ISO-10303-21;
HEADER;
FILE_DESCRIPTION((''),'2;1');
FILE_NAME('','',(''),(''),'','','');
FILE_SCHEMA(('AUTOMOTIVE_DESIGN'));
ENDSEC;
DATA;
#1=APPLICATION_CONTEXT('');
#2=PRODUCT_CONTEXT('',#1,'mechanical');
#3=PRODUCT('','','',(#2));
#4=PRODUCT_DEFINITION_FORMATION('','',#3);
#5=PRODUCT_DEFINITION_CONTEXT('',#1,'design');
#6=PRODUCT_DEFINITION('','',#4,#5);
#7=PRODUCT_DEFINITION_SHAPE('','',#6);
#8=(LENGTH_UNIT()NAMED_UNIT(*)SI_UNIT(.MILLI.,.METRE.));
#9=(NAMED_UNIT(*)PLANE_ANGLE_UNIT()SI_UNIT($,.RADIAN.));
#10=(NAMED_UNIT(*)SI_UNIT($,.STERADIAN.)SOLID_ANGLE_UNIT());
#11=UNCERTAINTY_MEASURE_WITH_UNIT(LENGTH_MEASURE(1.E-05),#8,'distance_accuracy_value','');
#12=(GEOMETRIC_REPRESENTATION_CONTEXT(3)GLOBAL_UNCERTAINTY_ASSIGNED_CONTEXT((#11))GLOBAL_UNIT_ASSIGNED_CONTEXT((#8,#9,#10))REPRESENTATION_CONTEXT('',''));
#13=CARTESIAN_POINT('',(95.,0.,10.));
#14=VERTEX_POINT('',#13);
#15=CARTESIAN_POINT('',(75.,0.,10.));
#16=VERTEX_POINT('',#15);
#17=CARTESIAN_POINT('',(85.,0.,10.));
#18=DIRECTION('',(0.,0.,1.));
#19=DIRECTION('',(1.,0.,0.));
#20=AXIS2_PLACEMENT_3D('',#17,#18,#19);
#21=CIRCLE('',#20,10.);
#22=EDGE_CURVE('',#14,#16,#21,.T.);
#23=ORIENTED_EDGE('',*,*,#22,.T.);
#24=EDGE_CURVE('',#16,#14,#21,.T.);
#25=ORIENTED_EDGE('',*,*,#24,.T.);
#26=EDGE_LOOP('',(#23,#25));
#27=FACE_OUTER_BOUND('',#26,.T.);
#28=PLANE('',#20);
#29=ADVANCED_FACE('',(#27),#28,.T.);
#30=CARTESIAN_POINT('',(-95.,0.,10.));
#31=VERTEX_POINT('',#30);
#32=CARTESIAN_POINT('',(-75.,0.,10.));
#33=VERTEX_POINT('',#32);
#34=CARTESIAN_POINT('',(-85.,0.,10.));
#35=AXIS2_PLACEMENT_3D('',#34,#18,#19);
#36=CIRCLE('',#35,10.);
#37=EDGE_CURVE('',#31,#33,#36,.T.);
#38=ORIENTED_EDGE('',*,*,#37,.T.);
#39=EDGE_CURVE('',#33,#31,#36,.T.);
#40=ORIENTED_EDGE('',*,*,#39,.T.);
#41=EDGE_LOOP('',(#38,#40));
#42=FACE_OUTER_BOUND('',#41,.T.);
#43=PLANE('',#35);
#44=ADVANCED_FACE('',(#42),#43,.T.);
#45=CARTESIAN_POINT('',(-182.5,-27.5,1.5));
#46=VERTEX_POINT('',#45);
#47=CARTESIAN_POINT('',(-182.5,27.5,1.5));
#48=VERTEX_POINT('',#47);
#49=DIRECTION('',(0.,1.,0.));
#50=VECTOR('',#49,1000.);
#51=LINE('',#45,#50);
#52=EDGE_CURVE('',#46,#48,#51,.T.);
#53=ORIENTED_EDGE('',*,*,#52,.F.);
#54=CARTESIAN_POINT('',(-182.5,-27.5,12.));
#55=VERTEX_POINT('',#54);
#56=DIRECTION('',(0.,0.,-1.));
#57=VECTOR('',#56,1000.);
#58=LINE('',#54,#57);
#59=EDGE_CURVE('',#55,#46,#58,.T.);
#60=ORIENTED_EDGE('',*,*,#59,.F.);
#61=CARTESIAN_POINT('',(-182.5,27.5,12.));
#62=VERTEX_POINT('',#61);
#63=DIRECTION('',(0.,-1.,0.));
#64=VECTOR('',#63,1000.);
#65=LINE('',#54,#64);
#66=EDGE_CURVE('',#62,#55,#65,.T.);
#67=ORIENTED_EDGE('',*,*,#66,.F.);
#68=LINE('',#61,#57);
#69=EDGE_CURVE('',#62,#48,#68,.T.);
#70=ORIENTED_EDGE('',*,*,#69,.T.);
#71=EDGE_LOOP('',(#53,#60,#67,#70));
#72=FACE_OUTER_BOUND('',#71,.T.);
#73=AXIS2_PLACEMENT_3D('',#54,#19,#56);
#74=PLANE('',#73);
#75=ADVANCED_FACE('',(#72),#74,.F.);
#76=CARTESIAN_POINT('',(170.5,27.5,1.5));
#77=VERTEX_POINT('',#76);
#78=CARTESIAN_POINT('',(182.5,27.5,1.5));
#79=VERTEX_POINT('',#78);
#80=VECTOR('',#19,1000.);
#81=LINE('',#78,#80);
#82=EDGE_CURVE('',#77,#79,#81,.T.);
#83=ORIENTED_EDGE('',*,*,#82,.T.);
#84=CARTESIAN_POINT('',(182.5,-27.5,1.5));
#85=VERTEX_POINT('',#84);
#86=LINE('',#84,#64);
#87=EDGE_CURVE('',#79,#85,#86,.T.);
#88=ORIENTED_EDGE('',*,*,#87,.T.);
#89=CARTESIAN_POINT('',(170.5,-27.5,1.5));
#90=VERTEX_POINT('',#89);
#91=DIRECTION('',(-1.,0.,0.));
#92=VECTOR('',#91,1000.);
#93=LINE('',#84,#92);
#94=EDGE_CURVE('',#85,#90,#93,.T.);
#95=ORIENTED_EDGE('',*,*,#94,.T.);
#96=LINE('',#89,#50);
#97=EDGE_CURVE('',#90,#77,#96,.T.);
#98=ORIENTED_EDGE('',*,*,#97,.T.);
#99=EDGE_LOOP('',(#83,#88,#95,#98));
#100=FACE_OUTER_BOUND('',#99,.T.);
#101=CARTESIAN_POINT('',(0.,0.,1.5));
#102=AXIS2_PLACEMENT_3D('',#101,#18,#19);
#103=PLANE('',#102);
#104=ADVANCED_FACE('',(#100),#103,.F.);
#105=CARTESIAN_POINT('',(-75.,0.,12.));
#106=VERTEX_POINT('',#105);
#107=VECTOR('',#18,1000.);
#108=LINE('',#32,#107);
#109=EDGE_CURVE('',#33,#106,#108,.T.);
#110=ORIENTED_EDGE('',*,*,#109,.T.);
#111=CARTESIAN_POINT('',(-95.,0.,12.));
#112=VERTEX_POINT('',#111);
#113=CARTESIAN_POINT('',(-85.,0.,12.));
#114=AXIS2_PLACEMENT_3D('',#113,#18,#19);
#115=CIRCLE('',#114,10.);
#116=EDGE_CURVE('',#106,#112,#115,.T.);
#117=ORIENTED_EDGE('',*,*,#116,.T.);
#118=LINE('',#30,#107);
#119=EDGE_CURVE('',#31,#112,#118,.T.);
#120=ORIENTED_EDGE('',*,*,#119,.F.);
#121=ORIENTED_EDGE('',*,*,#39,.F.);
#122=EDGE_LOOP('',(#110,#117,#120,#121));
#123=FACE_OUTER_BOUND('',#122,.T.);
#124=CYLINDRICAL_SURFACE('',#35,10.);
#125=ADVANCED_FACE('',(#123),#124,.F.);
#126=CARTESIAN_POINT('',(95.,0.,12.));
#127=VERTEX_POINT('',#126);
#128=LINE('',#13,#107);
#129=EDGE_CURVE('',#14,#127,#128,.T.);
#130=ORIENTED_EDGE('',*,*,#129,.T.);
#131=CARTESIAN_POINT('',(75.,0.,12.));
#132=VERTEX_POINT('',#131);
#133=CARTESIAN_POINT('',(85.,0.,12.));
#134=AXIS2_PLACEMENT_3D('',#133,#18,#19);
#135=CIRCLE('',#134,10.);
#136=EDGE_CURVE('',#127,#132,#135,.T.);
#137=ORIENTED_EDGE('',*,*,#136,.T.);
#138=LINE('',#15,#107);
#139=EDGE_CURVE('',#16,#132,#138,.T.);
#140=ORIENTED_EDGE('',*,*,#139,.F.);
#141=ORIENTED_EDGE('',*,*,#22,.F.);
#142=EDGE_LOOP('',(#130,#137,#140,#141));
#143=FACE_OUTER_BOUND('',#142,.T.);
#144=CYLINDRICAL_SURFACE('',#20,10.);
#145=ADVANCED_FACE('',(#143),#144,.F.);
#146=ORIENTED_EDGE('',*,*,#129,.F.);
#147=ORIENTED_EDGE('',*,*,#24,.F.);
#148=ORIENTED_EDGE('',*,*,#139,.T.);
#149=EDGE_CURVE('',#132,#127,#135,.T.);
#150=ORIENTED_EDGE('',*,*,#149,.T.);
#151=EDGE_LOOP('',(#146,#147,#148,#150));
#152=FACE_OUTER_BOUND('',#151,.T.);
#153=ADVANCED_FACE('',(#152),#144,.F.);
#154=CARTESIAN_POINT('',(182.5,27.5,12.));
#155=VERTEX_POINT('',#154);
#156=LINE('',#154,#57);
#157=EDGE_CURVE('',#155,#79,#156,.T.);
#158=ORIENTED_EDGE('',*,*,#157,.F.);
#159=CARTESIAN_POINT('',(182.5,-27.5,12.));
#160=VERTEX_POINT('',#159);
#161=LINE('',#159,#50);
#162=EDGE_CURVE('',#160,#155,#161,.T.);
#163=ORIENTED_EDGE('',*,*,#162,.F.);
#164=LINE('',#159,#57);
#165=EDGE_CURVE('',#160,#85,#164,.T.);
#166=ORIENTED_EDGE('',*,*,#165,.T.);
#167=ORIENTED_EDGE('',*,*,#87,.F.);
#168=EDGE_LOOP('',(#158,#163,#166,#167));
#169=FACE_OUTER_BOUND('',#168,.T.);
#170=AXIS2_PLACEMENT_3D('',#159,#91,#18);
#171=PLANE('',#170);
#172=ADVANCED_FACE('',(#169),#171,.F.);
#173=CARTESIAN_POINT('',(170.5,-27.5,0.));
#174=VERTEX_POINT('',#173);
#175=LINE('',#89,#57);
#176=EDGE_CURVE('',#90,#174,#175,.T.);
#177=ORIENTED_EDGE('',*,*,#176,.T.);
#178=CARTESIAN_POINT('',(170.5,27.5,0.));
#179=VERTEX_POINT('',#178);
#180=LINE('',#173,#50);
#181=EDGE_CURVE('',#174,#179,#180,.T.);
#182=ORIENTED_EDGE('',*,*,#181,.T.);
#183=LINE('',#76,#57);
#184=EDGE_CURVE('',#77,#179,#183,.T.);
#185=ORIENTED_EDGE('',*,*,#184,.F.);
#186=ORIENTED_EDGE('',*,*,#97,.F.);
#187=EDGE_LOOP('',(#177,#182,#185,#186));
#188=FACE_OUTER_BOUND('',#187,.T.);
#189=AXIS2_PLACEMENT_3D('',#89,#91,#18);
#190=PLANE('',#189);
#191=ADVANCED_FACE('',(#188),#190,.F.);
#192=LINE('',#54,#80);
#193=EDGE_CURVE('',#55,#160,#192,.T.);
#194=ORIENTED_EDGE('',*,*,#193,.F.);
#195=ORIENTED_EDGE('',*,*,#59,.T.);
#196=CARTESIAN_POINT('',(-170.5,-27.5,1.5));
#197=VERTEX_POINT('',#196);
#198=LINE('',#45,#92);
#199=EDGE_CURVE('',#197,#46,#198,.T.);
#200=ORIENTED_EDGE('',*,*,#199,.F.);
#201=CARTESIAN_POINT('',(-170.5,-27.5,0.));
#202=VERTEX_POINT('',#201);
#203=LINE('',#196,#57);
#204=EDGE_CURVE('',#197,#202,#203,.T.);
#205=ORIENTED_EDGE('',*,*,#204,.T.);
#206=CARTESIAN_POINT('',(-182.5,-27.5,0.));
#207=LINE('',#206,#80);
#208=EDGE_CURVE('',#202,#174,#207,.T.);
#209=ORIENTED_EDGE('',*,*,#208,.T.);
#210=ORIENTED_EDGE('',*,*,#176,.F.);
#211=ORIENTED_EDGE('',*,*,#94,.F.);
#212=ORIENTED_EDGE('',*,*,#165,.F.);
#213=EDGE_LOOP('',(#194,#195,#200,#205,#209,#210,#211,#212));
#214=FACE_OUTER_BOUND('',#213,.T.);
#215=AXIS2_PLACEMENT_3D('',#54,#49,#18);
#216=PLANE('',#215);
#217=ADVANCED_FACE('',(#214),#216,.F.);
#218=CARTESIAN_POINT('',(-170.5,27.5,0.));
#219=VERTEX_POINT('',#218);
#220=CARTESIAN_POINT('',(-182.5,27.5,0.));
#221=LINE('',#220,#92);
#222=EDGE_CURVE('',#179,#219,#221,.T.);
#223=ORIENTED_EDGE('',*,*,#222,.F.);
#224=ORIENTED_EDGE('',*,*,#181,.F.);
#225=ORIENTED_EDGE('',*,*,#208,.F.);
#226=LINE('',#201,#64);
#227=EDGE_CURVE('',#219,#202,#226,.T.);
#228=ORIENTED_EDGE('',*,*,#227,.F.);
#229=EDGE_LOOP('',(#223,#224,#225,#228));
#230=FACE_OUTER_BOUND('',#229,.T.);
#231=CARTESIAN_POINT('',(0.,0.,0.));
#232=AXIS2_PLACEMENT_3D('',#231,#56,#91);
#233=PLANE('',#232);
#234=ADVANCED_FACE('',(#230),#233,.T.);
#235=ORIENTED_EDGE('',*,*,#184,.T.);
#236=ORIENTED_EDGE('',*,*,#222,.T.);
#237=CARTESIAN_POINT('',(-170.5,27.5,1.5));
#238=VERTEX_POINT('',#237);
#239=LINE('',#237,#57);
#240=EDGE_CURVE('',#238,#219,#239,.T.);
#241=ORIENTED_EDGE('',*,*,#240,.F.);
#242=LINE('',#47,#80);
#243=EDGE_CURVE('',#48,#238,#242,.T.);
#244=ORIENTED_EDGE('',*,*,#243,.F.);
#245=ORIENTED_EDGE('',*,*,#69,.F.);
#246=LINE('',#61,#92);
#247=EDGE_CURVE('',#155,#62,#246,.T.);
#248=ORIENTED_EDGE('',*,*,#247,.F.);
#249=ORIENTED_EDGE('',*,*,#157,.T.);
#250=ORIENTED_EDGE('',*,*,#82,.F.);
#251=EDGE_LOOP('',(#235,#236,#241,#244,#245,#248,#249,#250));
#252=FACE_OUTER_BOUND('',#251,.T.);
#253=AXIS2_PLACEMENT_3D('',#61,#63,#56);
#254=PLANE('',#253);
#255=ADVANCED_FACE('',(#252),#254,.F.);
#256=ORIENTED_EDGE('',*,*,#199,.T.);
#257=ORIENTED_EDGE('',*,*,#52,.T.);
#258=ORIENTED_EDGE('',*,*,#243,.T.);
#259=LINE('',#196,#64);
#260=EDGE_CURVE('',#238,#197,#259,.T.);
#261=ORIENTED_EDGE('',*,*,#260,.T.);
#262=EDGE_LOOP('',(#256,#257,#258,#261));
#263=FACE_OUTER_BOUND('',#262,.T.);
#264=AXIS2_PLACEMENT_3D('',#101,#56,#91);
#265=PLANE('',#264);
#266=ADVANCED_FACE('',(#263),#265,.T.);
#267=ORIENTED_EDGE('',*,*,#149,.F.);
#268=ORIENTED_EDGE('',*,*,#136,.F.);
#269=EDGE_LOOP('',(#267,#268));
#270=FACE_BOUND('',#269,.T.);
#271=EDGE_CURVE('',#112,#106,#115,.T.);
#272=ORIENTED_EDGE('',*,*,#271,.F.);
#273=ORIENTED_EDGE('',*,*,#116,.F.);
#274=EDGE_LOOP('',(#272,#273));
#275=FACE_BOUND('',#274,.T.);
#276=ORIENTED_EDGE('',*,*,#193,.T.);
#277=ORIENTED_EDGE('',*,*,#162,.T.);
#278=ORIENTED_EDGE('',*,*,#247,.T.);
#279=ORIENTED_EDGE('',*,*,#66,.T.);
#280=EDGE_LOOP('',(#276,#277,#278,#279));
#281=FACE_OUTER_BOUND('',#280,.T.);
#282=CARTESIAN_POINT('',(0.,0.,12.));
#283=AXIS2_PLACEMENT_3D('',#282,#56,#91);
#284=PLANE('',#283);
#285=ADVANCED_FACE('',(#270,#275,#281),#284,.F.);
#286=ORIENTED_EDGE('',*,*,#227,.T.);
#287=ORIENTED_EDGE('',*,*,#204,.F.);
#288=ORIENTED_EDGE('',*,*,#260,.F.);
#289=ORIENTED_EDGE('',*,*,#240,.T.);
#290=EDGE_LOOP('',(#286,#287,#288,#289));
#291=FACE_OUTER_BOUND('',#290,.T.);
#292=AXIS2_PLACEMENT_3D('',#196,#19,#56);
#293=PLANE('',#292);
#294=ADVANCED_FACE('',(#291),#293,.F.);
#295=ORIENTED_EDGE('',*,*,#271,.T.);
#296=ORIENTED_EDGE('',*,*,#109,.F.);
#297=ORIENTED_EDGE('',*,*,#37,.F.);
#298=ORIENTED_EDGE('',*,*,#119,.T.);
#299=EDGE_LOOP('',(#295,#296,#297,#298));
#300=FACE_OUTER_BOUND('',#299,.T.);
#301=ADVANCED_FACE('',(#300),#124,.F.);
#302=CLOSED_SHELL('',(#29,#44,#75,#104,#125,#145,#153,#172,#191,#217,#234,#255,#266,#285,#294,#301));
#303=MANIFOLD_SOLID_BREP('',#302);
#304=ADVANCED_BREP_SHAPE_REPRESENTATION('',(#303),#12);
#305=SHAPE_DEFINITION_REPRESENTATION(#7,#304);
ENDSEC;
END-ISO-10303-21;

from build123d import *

# Parameters (mm, degrees)
SKETCH_1_W          = 365
SKETCH_1_H          = 55
EXTRUDE_1_DEPTH     = 12
SKETCH_2_R          = 10
CUT_EXTRUDE_1_DEPTH = 2
SKETCH_3_W          = 12
SKETCH_3_H          = 55
CUT_EXTRUDE_2_DEPTH = 1.5


with BuildPart() as part:
    # 草图1 → 凸台-拉伸1 (new body)
    with BuildSketch(Plane.XY):
        Rectangle(SKETCH_1_W, SKETCH_1_H)
    extrude(amount=EXTRUDE_1_DEPTH)

    # 草图2 → 切除-拉伸1 (cut)
    with BuildSketch(Plane.XY.offset(12)):
        with Locations((85, 0)):
            Circle(SKETCH_2_R)
        with Locations((-85, 0)):
            Circle(SKETCH_2_R)
    extrude(amount=-CUT_EXTRUDE_1_DEPTH, mode=Mode.SUBTRACT)

    # 草图3 → 切除-拉伸2 (cut)
    with BuildSketch(Plane(origin=(0, 0, 0), x_dir=(-1, 0, 0), z_dir=(0, 0, -1))):
        with Locations((176.5, 0)):
            Rectangle(SKETCH_3_W, SKETCH_3_H)
        with Locations((-176.5, 0)):
            Rectangle(SKETCH_3_W, SKETCH_3_H)
    extrude(amount=-CUT_EXTRUDE_2_DEPTH, mode=Mode.SUBTRACT)


solid = part.part
